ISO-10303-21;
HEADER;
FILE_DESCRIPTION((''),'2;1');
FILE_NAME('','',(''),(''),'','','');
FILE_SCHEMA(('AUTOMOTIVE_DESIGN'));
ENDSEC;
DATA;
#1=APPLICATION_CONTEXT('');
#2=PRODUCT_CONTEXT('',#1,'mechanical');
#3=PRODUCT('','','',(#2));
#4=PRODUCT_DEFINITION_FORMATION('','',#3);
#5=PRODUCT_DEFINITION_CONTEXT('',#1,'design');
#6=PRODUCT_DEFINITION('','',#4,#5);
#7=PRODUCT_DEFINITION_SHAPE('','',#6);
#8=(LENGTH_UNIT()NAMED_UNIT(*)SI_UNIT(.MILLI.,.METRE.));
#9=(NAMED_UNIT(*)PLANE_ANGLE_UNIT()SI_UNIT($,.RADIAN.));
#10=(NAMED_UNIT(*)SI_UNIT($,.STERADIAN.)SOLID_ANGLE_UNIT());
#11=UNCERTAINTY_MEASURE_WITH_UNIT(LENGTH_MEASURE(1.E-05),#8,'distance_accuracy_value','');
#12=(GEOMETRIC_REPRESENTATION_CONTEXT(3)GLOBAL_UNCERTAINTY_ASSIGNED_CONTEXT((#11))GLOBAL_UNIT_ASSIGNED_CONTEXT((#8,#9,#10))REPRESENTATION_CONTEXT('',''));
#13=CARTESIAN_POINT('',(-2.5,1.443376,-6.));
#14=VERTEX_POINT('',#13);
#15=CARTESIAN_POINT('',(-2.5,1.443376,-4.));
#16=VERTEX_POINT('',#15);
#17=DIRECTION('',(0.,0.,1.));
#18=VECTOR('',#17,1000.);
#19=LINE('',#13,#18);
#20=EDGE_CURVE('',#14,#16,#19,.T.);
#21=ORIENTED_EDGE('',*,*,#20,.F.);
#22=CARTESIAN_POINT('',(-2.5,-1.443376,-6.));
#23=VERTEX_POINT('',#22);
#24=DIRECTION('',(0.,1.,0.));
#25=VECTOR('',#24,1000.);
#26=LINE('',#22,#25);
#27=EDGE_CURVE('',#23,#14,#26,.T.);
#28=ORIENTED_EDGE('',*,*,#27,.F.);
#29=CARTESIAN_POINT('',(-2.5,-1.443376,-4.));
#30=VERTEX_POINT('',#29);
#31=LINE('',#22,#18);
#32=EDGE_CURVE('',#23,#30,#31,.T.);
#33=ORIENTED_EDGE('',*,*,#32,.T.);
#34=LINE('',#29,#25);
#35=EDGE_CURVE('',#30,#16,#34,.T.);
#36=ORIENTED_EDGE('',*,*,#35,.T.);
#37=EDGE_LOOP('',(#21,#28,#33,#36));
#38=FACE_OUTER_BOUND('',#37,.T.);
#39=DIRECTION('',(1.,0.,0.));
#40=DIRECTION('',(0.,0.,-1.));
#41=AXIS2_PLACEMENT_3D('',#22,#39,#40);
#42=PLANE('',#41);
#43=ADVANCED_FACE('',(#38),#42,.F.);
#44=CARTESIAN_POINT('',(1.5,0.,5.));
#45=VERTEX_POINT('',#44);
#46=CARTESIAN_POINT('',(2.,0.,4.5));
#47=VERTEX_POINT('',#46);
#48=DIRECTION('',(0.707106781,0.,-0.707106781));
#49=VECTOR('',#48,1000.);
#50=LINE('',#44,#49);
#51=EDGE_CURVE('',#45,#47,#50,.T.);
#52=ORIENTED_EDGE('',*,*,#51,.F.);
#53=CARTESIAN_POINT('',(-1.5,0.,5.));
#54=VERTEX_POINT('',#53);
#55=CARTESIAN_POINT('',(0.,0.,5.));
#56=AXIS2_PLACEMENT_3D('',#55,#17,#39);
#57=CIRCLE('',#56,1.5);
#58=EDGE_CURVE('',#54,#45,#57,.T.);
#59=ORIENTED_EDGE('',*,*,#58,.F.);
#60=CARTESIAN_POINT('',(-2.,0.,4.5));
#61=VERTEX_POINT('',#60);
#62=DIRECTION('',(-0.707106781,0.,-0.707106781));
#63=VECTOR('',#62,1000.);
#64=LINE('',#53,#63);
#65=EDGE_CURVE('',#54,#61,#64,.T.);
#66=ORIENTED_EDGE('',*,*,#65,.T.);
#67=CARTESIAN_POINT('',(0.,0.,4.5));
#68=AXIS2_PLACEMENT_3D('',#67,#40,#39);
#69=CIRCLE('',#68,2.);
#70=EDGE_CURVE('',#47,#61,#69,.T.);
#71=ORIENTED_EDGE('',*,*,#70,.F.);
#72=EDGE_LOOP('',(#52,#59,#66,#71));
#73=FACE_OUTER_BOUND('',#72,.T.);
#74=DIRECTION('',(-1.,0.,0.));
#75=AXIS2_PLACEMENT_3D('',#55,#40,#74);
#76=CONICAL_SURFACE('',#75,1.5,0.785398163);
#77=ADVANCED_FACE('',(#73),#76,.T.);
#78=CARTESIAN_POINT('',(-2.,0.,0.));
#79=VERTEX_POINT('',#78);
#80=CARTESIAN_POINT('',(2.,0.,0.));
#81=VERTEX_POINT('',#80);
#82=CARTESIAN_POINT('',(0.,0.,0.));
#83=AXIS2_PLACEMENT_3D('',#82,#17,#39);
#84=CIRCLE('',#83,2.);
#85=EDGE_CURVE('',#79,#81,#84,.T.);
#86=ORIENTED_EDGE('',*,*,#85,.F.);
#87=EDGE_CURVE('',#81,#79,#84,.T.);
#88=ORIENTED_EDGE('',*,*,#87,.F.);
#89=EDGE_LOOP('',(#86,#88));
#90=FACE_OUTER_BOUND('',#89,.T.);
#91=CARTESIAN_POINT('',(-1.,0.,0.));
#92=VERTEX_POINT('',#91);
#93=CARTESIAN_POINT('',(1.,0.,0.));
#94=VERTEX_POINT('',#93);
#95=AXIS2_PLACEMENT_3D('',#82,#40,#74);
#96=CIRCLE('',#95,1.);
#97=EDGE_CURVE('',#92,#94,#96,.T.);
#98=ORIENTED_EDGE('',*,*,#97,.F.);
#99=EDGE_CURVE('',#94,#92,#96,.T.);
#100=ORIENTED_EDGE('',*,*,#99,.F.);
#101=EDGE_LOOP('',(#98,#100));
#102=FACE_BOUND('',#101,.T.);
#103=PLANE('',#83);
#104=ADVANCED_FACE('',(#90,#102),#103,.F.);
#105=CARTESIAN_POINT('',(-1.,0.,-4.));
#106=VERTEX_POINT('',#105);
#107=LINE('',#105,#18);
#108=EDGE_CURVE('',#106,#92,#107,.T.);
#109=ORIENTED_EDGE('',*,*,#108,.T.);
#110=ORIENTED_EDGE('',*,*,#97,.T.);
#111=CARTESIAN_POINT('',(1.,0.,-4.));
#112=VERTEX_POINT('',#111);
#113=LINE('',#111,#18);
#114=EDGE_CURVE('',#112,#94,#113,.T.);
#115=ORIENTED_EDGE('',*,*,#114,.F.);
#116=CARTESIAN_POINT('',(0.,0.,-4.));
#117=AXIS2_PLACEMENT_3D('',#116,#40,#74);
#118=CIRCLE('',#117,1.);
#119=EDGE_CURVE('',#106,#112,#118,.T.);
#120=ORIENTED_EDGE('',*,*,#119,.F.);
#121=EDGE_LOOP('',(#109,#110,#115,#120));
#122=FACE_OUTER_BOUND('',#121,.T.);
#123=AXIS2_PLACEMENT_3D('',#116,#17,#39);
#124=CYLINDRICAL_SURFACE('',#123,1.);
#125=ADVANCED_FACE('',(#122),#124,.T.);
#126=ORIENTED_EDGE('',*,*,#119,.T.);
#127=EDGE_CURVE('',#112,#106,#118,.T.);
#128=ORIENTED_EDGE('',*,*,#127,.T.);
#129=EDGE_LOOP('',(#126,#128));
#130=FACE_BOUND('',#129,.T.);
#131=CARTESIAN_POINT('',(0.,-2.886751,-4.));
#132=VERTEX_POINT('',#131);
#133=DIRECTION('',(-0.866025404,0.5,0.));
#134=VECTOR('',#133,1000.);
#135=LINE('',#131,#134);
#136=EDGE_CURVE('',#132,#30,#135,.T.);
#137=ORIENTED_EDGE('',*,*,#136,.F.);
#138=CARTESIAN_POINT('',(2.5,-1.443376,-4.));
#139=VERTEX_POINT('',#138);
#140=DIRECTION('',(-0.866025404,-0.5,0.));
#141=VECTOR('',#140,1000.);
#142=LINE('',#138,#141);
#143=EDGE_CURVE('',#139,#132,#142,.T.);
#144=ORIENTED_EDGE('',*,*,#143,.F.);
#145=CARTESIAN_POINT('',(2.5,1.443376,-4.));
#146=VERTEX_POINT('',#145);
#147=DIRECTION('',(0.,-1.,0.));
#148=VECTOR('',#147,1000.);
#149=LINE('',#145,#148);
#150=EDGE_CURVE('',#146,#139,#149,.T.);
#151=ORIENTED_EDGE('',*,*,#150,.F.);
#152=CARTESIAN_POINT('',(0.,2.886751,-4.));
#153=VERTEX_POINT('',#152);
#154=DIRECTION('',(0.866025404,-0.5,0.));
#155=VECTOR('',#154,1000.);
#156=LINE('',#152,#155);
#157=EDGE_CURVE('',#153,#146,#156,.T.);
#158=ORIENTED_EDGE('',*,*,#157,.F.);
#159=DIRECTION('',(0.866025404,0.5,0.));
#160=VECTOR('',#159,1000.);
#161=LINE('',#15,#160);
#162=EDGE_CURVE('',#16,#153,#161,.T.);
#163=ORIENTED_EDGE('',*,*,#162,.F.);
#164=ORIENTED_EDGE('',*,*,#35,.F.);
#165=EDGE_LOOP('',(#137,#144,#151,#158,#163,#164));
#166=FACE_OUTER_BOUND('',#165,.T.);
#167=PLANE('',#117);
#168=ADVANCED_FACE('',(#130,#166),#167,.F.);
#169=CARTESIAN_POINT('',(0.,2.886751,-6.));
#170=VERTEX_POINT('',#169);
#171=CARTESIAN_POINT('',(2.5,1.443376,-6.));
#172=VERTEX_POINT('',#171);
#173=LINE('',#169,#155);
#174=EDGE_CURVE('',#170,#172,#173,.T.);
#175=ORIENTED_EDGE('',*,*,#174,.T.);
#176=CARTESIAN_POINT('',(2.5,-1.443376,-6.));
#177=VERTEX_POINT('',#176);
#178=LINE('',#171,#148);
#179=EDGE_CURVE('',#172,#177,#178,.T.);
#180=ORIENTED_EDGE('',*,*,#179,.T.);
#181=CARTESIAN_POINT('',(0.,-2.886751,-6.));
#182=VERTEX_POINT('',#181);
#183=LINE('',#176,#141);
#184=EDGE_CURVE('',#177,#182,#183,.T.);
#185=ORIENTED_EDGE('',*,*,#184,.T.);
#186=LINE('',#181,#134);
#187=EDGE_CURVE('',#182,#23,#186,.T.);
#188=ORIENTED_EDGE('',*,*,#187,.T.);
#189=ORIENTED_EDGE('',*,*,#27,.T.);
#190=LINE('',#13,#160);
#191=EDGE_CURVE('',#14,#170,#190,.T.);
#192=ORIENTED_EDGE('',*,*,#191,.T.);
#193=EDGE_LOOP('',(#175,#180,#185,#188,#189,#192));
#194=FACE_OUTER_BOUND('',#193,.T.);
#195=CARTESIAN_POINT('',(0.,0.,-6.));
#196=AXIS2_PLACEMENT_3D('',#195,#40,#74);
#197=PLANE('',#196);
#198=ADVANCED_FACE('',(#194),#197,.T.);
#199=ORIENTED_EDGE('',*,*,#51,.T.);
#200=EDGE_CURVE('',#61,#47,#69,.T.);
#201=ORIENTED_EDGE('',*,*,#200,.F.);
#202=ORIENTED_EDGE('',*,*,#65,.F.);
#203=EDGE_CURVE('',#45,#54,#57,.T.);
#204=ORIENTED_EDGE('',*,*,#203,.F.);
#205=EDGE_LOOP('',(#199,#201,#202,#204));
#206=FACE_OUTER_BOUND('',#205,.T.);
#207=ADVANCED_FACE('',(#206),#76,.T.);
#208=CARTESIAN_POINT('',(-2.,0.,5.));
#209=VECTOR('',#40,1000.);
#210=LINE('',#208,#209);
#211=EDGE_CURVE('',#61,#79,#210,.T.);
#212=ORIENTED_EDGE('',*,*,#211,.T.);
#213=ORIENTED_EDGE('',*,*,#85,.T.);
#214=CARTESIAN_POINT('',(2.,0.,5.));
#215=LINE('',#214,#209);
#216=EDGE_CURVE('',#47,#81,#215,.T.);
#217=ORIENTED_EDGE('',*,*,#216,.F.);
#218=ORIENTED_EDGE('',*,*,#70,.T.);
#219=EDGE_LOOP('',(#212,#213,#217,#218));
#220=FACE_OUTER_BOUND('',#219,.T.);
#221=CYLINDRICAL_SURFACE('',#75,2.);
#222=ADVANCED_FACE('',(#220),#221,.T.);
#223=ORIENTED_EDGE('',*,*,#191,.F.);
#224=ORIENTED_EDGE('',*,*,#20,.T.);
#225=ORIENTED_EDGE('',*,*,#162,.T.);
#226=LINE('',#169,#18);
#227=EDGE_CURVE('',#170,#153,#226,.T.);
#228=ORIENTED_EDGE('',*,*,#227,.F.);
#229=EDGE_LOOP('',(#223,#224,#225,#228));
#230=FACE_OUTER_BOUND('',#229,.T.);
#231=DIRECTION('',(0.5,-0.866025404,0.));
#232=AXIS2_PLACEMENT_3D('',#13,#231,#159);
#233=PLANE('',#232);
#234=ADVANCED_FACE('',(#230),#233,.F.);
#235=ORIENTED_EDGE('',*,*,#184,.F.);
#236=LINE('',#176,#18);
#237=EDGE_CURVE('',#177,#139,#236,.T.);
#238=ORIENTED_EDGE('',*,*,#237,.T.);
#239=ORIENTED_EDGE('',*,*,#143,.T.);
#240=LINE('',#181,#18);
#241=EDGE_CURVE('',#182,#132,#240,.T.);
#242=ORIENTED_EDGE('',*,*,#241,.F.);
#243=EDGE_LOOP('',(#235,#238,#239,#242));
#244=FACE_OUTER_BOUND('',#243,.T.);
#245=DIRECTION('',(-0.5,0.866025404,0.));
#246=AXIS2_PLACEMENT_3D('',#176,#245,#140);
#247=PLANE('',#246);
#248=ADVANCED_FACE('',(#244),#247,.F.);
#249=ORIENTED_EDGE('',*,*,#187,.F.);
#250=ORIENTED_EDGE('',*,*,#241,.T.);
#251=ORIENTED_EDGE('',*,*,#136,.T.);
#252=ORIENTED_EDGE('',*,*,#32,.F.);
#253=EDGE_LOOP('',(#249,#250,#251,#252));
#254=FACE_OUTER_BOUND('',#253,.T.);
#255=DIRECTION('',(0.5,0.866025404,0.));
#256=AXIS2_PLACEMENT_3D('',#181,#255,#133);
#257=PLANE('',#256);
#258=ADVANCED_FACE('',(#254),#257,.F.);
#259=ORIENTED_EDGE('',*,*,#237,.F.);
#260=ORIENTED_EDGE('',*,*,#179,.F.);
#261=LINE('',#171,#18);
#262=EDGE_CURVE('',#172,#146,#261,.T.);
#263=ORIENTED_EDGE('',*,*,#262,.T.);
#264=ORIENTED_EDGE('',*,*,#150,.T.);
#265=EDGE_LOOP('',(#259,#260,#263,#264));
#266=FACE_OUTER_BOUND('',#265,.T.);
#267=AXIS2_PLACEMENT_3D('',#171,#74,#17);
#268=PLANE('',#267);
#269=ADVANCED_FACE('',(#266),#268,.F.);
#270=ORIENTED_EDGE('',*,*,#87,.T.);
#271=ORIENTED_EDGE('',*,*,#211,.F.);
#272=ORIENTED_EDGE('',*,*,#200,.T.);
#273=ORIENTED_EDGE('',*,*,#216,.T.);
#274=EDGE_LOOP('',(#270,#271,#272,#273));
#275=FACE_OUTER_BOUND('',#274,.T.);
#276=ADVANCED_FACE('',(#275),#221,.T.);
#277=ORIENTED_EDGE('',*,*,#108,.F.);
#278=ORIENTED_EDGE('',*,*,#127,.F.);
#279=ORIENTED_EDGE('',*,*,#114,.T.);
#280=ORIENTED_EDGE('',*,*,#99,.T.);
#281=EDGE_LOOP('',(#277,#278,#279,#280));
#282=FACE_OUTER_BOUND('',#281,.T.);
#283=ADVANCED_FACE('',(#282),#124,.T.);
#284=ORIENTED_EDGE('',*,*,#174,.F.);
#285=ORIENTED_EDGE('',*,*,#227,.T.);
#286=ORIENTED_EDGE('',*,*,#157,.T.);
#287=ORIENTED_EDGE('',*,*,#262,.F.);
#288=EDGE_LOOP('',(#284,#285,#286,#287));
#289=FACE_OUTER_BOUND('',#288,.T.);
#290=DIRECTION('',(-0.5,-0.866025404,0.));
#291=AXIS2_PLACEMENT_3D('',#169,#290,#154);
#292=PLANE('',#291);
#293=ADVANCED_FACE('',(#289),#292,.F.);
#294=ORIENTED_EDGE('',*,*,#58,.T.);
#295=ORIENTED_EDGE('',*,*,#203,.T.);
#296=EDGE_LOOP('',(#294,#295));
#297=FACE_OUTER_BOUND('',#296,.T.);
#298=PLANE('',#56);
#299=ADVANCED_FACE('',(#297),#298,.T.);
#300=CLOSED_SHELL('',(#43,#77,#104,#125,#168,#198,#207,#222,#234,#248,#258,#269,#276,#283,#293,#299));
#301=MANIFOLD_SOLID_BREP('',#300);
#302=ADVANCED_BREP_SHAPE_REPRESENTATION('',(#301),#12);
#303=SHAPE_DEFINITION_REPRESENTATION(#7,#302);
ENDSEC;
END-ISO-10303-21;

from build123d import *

# Parameters (mm, degrees)
SKETCH1_R           = 2
BOSS_EXTRUDE1_DEPTH = 5
SKETCH2_R           = 1
BOSS_EXTRUDE2_DEPTH = 4
BOSS_EXTRUDE3_DEPTH = 2
CHAMFER1_SIZE       = 0.5


with BuildPart() as part:
    # Sketch1 → Boss-Extrude1 (new body)
    with BuildSketch(Plane.XY):
        Circle(SKETCH1_R)
    extrude(amount=BOSS_EXTRUDE1_DEPTH)

    # Sketch2 → Boss-Extrude2 (add)
    with BuildSketch(Plane(origin=(0, 0, 0), x_dir=(-1, 0, 0), z_dir=(0, 0, -1))):
        Circle(SKETCH2_R)
    extrude(amount=BOSS_EXTRUDE2_DEPTH)

    # Sketch3 → Boss-Extrude3 (add)
    with BuildSketch(Plane(origin=(0, 0, -4), x_dir=(-1, 0, 0), z_dir=(0, 0, -1))):
        Polygon((0, 2.886751346), (-2.5, 1.443375673), (-2.5, -1.443375673), (0, -2.886751346), (2.5, -1.443375673), (2.5, 1.443375673), align=None)
    extrude(amount=BOSS_EXTRUDE3_DEPTH)

    # Chamfer1
    chamfer1_edges = [part.edges().sort_by_distance(p)[0] for p in [
        (-2, 0, 5),
    ]]
    chamfer(chamfer1_edges, length=CHAMFER1_SIZE)


solid = part.part
